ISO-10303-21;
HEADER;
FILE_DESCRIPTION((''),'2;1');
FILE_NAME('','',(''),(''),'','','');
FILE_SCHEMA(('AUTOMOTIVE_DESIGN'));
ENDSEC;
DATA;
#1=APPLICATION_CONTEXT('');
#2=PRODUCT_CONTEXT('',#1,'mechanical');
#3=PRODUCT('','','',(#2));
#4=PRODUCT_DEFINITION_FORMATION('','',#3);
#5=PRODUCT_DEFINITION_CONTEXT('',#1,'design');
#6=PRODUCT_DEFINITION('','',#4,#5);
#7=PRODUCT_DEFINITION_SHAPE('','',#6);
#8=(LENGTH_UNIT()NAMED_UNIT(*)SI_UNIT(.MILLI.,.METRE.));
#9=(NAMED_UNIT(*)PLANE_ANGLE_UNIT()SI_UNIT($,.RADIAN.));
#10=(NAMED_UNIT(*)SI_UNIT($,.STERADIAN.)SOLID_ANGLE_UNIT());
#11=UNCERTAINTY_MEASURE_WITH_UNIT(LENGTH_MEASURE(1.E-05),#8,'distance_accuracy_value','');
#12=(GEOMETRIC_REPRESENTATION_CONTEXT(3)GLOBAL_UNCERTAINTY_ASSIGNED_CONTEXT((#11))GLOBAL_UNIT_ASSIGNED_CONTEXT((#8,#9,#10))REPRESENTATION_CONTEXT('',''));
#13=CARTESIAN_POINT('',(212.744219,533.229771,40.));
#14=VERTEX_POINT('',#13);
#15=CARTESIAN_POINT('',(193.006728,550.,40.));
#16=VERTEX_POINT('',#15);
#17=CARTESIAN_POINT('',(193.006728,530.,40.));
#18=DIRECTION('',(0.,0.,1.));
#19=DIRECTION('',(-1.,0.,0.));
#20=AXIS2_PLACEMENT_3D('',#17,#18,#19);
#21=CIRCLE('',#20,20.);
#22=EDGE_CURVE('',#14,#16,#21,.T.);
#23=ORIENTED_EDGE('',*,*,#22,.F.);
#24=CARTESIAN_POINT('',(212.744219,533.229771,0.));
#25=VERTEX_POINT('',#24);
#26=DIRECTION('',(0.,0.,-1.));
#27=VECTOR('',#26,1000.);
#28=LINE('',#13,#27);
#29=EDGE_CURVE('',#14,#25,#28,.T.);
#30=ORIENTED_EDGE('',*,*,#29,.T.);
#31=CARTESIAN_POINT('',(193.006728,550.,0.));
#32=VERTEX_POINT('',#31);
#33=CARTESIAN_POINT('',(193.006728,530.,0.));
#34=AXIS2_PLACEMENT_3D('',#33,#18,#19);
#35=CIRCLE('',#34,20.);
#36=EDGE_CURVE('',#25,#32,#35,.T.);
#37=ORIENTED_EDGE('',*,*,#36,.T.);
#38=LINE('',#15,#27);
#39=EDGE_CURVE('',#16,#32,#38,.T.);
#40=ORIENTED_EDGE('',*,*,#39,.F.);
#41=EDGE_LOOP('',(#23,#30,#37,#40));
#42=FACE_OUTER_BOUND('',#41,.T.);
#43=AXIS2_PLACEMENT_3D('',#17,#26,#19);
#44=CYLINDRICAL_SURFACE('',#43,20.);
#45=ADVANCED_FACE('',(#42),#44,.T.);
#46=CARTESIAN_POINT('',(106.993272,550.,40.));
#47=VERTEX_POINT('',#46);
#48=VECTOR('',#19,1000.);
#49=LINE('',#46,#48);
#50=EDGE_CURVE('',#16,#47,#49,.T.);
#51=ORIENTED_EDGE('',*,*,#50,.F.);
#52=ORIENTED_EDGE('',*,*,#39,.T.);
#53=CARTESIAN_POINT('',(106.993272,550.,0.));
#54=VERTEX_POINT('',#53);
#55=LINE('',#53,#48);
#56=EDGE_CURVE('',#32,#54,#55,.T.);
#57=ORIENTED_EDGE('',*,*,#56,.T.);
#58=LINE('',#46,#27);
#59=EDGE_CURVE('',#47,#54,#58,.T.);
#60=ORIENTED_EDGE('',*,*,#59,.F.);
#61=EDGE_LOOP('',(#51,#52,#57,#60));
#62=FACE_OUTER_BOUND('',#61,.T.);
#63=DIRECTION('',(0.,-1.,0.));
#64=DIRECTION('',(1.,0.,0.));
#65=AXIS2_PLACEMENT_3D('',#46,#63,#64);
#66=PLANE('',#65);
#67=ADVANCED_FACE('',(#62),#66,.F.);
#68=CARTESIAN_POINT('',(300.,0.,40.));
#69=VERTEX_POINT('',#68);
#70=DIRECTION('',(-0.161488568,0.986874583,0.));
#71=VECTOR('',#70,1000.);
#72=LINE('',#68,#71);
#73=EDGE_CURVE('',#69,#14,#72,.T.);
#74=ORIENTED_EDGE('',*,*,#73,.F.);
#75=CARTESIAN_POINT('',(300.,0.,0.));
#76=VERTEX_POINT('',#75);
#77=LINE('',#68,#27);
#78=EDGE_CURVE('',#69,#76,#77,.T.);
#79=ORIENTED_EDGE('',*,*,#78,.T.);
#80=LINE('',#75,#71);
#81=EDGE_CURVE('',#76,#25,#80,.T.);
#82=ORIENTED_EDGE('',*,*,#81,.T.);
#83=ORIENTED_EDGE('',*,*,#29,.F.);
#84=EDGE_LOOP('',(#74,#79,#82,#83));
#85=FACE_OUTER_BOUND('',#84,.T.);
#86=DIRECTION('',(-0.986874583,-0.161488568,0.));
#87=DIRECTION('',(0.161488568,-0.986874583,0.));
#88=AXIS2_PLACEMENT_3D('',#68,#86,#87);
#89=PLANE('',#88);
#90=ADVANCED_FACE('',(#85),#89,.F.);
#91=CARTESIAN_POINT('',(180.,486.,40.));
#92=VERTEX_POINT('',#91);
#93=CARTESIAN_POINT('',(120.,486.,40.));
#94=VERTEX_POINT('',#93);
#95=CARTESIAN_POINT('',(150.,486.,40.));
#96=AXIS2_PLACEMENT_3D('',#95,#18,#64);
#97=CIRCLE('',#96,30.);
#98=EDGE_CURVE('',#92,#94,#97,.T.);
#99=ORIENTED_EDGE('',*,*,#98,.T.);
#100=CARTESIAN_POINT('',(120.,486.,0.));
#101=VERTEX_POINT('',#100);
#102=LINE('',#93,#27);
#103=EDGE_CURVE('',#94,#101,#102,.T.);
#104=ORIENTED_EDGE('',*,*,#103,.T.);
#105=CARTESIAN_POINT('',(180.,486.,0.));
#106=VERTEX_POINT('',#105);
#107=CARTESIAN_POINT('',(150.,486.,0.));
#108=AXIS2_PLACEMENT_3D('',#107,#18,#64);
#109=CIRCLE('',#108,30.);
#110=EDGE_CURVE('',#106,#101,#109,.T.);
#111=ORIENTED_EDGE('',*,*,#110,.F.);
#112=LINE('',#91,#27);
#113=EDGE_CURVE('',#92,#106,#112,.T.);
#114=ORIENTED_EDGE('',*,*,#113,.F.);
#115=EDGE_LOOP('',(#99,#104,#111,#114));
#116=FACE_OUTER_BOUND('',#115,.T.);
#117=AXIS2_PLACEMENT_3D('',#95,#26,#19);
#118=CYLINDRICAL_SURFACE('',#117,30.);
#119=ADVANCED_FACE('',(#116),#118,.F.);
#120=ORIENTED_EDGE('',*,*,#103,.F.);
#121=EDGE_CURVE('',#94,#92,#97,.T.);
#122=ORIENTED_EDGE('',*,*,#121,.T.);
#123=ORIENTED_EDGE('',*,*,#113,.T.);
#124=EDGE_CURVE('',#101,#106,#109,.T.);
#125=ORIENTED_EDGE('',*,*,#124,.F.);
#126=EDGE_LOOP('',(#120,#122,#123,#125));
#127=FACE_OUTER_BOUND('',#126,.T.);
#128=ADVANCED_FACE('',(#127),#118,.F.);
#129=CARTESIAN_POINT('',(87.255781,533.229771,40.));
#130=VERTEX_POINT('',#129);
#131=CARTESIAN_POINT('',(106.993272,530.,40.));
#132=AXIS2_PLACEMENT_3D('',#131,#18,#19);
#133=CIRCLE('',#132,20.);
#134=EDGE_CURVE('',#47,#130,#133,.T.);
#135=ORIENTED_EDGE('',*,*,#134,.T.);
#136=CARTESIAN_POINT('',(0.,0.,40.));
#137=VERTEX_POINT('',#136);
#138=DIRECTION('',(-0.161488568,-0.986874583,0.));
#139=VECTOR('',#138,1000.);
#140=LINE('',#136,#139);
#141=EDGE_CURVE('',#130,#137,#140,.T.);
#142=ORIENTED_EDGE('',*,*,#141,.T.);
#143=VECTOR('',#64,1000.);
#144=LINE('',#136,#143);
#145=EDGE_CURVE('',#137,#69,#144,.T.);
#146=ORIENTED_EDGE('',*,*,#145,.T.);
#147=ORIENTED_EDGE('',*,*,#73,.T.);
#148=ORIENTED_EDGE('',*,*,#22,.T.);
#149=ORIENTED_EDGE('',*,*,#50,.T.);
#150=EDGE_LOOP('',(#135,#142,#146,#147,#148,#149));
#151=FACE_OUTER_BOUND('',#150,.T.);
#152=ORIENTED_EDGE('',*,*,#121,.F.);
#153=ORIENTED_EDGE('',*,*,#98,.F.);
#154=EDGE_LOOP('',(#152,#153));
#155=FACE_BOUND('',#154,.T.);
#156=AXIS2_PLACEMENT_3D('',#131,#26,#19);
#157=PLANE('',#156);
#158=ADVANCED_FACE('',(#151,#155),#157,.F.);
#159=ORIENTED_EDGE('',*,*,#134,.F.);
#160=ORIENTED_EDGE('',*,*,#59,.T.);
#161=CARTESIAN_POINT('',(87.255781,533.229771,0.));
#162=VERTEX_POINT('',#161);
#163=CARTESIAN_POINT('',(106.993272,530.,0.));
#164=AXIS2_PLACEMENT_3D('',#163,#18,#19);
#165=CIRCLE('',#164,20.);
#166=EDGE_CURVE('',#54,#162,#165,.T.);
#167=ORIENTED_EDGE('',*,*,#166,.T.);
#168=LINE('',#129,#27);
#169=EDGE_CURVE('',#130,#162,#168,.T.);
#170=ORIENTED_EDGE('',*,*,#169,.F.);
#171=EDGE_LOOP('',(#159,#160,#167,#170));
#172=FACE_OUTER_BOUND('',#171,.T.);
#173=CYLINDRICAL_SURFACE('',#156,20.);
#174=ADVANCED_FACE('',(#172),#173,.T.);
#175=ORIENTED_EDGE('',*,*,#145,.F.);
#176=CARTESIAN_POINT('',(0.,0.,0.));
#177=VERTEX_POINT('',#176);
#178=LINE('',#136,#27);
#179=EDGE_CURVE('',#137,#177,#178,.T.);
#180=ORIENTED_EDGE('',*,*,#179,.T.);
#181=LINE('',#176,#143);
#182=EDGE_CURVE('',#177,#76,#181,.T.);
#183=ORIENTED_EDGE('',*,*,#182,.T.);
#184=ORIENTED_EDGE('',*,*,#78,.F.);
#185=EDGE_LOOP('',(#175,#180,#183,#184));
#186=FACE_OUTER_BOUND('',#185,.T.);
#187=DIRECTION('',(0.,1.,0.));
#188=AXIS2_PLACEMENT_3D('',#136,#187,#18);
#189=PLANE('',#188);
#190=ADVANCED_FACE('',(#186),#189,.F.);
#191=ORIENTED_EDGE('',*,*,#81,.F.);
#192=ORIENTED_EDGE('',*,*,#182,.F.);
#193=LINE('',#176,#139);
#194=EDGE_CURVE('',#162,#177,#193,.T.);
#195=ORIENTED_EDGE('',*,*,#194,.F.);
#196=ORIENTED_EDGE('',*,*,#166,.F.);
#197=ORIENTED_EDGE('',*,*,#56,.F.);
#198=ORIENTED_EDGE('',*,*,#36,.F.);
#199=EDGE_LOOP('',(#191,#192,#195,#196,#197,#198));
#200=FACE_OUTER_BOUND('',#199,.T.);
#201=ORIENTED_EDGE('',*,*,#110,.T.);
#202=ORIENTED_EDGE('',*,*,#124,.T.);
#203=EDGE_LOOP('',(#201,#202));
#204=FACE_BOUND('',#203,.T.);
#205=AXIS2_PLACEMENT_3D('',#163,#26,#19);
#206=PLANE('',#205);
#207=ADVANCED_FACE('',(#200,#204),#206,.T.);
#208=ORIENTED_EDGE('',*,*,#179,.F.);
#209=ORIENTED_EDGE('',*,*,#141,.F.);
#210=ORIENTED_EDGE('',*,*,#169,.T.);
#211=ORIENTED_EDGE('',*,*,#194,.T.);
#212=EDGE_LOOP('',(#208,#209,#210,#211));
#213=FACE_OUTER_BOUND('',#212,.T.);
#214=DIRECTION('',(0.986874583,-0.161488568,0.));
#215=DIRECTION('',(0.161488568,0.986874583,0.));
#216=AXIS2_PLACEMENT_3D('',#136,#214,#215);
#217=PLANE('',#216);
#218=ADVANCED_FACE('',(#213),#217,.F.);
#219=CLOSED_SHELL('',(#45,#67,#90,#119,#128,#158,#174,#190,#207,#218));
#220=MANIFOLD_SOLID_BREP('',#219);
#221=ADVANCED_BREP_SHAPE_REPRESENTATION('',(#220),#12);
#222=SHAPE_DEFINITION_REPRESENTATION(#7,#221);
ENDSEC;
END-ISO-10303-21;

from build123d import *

# Parameters (mm, degrees)
SKETCH1_R           = 30
BOSS_EXTRUDE1_DEPTH = 40


with BuildPart() as part:
    # Sketch1 → Boss-Extrude1 (new body)
    with BuildSketch(Plane.XY):
        with BuildLine():
            Line((0, 0), (300, 0))
            Line((300, 0), (212.744219232, 533.229771362))
            ThreePointArc((212.744219232, 533.229771362), (205.956719326, 545.241316007), (193.006727574, 550))
            Line((193.006727574, 550), (106.993272426, 550))
            ThreePointArc((106.993272426, 550), (94.043280674, 545.241316007), (87.255780768, 533.229771362))
            Line((87.255780768, 533.229771362), (0, 0))
        make_face()
        with Locations((150, 486)):
            Circle(SKETCH1_R, mode=Mode.SUBTRACT)
    extrude(amount=BOSS_EXTRUDE1_DEPTH)


solid = part.part
